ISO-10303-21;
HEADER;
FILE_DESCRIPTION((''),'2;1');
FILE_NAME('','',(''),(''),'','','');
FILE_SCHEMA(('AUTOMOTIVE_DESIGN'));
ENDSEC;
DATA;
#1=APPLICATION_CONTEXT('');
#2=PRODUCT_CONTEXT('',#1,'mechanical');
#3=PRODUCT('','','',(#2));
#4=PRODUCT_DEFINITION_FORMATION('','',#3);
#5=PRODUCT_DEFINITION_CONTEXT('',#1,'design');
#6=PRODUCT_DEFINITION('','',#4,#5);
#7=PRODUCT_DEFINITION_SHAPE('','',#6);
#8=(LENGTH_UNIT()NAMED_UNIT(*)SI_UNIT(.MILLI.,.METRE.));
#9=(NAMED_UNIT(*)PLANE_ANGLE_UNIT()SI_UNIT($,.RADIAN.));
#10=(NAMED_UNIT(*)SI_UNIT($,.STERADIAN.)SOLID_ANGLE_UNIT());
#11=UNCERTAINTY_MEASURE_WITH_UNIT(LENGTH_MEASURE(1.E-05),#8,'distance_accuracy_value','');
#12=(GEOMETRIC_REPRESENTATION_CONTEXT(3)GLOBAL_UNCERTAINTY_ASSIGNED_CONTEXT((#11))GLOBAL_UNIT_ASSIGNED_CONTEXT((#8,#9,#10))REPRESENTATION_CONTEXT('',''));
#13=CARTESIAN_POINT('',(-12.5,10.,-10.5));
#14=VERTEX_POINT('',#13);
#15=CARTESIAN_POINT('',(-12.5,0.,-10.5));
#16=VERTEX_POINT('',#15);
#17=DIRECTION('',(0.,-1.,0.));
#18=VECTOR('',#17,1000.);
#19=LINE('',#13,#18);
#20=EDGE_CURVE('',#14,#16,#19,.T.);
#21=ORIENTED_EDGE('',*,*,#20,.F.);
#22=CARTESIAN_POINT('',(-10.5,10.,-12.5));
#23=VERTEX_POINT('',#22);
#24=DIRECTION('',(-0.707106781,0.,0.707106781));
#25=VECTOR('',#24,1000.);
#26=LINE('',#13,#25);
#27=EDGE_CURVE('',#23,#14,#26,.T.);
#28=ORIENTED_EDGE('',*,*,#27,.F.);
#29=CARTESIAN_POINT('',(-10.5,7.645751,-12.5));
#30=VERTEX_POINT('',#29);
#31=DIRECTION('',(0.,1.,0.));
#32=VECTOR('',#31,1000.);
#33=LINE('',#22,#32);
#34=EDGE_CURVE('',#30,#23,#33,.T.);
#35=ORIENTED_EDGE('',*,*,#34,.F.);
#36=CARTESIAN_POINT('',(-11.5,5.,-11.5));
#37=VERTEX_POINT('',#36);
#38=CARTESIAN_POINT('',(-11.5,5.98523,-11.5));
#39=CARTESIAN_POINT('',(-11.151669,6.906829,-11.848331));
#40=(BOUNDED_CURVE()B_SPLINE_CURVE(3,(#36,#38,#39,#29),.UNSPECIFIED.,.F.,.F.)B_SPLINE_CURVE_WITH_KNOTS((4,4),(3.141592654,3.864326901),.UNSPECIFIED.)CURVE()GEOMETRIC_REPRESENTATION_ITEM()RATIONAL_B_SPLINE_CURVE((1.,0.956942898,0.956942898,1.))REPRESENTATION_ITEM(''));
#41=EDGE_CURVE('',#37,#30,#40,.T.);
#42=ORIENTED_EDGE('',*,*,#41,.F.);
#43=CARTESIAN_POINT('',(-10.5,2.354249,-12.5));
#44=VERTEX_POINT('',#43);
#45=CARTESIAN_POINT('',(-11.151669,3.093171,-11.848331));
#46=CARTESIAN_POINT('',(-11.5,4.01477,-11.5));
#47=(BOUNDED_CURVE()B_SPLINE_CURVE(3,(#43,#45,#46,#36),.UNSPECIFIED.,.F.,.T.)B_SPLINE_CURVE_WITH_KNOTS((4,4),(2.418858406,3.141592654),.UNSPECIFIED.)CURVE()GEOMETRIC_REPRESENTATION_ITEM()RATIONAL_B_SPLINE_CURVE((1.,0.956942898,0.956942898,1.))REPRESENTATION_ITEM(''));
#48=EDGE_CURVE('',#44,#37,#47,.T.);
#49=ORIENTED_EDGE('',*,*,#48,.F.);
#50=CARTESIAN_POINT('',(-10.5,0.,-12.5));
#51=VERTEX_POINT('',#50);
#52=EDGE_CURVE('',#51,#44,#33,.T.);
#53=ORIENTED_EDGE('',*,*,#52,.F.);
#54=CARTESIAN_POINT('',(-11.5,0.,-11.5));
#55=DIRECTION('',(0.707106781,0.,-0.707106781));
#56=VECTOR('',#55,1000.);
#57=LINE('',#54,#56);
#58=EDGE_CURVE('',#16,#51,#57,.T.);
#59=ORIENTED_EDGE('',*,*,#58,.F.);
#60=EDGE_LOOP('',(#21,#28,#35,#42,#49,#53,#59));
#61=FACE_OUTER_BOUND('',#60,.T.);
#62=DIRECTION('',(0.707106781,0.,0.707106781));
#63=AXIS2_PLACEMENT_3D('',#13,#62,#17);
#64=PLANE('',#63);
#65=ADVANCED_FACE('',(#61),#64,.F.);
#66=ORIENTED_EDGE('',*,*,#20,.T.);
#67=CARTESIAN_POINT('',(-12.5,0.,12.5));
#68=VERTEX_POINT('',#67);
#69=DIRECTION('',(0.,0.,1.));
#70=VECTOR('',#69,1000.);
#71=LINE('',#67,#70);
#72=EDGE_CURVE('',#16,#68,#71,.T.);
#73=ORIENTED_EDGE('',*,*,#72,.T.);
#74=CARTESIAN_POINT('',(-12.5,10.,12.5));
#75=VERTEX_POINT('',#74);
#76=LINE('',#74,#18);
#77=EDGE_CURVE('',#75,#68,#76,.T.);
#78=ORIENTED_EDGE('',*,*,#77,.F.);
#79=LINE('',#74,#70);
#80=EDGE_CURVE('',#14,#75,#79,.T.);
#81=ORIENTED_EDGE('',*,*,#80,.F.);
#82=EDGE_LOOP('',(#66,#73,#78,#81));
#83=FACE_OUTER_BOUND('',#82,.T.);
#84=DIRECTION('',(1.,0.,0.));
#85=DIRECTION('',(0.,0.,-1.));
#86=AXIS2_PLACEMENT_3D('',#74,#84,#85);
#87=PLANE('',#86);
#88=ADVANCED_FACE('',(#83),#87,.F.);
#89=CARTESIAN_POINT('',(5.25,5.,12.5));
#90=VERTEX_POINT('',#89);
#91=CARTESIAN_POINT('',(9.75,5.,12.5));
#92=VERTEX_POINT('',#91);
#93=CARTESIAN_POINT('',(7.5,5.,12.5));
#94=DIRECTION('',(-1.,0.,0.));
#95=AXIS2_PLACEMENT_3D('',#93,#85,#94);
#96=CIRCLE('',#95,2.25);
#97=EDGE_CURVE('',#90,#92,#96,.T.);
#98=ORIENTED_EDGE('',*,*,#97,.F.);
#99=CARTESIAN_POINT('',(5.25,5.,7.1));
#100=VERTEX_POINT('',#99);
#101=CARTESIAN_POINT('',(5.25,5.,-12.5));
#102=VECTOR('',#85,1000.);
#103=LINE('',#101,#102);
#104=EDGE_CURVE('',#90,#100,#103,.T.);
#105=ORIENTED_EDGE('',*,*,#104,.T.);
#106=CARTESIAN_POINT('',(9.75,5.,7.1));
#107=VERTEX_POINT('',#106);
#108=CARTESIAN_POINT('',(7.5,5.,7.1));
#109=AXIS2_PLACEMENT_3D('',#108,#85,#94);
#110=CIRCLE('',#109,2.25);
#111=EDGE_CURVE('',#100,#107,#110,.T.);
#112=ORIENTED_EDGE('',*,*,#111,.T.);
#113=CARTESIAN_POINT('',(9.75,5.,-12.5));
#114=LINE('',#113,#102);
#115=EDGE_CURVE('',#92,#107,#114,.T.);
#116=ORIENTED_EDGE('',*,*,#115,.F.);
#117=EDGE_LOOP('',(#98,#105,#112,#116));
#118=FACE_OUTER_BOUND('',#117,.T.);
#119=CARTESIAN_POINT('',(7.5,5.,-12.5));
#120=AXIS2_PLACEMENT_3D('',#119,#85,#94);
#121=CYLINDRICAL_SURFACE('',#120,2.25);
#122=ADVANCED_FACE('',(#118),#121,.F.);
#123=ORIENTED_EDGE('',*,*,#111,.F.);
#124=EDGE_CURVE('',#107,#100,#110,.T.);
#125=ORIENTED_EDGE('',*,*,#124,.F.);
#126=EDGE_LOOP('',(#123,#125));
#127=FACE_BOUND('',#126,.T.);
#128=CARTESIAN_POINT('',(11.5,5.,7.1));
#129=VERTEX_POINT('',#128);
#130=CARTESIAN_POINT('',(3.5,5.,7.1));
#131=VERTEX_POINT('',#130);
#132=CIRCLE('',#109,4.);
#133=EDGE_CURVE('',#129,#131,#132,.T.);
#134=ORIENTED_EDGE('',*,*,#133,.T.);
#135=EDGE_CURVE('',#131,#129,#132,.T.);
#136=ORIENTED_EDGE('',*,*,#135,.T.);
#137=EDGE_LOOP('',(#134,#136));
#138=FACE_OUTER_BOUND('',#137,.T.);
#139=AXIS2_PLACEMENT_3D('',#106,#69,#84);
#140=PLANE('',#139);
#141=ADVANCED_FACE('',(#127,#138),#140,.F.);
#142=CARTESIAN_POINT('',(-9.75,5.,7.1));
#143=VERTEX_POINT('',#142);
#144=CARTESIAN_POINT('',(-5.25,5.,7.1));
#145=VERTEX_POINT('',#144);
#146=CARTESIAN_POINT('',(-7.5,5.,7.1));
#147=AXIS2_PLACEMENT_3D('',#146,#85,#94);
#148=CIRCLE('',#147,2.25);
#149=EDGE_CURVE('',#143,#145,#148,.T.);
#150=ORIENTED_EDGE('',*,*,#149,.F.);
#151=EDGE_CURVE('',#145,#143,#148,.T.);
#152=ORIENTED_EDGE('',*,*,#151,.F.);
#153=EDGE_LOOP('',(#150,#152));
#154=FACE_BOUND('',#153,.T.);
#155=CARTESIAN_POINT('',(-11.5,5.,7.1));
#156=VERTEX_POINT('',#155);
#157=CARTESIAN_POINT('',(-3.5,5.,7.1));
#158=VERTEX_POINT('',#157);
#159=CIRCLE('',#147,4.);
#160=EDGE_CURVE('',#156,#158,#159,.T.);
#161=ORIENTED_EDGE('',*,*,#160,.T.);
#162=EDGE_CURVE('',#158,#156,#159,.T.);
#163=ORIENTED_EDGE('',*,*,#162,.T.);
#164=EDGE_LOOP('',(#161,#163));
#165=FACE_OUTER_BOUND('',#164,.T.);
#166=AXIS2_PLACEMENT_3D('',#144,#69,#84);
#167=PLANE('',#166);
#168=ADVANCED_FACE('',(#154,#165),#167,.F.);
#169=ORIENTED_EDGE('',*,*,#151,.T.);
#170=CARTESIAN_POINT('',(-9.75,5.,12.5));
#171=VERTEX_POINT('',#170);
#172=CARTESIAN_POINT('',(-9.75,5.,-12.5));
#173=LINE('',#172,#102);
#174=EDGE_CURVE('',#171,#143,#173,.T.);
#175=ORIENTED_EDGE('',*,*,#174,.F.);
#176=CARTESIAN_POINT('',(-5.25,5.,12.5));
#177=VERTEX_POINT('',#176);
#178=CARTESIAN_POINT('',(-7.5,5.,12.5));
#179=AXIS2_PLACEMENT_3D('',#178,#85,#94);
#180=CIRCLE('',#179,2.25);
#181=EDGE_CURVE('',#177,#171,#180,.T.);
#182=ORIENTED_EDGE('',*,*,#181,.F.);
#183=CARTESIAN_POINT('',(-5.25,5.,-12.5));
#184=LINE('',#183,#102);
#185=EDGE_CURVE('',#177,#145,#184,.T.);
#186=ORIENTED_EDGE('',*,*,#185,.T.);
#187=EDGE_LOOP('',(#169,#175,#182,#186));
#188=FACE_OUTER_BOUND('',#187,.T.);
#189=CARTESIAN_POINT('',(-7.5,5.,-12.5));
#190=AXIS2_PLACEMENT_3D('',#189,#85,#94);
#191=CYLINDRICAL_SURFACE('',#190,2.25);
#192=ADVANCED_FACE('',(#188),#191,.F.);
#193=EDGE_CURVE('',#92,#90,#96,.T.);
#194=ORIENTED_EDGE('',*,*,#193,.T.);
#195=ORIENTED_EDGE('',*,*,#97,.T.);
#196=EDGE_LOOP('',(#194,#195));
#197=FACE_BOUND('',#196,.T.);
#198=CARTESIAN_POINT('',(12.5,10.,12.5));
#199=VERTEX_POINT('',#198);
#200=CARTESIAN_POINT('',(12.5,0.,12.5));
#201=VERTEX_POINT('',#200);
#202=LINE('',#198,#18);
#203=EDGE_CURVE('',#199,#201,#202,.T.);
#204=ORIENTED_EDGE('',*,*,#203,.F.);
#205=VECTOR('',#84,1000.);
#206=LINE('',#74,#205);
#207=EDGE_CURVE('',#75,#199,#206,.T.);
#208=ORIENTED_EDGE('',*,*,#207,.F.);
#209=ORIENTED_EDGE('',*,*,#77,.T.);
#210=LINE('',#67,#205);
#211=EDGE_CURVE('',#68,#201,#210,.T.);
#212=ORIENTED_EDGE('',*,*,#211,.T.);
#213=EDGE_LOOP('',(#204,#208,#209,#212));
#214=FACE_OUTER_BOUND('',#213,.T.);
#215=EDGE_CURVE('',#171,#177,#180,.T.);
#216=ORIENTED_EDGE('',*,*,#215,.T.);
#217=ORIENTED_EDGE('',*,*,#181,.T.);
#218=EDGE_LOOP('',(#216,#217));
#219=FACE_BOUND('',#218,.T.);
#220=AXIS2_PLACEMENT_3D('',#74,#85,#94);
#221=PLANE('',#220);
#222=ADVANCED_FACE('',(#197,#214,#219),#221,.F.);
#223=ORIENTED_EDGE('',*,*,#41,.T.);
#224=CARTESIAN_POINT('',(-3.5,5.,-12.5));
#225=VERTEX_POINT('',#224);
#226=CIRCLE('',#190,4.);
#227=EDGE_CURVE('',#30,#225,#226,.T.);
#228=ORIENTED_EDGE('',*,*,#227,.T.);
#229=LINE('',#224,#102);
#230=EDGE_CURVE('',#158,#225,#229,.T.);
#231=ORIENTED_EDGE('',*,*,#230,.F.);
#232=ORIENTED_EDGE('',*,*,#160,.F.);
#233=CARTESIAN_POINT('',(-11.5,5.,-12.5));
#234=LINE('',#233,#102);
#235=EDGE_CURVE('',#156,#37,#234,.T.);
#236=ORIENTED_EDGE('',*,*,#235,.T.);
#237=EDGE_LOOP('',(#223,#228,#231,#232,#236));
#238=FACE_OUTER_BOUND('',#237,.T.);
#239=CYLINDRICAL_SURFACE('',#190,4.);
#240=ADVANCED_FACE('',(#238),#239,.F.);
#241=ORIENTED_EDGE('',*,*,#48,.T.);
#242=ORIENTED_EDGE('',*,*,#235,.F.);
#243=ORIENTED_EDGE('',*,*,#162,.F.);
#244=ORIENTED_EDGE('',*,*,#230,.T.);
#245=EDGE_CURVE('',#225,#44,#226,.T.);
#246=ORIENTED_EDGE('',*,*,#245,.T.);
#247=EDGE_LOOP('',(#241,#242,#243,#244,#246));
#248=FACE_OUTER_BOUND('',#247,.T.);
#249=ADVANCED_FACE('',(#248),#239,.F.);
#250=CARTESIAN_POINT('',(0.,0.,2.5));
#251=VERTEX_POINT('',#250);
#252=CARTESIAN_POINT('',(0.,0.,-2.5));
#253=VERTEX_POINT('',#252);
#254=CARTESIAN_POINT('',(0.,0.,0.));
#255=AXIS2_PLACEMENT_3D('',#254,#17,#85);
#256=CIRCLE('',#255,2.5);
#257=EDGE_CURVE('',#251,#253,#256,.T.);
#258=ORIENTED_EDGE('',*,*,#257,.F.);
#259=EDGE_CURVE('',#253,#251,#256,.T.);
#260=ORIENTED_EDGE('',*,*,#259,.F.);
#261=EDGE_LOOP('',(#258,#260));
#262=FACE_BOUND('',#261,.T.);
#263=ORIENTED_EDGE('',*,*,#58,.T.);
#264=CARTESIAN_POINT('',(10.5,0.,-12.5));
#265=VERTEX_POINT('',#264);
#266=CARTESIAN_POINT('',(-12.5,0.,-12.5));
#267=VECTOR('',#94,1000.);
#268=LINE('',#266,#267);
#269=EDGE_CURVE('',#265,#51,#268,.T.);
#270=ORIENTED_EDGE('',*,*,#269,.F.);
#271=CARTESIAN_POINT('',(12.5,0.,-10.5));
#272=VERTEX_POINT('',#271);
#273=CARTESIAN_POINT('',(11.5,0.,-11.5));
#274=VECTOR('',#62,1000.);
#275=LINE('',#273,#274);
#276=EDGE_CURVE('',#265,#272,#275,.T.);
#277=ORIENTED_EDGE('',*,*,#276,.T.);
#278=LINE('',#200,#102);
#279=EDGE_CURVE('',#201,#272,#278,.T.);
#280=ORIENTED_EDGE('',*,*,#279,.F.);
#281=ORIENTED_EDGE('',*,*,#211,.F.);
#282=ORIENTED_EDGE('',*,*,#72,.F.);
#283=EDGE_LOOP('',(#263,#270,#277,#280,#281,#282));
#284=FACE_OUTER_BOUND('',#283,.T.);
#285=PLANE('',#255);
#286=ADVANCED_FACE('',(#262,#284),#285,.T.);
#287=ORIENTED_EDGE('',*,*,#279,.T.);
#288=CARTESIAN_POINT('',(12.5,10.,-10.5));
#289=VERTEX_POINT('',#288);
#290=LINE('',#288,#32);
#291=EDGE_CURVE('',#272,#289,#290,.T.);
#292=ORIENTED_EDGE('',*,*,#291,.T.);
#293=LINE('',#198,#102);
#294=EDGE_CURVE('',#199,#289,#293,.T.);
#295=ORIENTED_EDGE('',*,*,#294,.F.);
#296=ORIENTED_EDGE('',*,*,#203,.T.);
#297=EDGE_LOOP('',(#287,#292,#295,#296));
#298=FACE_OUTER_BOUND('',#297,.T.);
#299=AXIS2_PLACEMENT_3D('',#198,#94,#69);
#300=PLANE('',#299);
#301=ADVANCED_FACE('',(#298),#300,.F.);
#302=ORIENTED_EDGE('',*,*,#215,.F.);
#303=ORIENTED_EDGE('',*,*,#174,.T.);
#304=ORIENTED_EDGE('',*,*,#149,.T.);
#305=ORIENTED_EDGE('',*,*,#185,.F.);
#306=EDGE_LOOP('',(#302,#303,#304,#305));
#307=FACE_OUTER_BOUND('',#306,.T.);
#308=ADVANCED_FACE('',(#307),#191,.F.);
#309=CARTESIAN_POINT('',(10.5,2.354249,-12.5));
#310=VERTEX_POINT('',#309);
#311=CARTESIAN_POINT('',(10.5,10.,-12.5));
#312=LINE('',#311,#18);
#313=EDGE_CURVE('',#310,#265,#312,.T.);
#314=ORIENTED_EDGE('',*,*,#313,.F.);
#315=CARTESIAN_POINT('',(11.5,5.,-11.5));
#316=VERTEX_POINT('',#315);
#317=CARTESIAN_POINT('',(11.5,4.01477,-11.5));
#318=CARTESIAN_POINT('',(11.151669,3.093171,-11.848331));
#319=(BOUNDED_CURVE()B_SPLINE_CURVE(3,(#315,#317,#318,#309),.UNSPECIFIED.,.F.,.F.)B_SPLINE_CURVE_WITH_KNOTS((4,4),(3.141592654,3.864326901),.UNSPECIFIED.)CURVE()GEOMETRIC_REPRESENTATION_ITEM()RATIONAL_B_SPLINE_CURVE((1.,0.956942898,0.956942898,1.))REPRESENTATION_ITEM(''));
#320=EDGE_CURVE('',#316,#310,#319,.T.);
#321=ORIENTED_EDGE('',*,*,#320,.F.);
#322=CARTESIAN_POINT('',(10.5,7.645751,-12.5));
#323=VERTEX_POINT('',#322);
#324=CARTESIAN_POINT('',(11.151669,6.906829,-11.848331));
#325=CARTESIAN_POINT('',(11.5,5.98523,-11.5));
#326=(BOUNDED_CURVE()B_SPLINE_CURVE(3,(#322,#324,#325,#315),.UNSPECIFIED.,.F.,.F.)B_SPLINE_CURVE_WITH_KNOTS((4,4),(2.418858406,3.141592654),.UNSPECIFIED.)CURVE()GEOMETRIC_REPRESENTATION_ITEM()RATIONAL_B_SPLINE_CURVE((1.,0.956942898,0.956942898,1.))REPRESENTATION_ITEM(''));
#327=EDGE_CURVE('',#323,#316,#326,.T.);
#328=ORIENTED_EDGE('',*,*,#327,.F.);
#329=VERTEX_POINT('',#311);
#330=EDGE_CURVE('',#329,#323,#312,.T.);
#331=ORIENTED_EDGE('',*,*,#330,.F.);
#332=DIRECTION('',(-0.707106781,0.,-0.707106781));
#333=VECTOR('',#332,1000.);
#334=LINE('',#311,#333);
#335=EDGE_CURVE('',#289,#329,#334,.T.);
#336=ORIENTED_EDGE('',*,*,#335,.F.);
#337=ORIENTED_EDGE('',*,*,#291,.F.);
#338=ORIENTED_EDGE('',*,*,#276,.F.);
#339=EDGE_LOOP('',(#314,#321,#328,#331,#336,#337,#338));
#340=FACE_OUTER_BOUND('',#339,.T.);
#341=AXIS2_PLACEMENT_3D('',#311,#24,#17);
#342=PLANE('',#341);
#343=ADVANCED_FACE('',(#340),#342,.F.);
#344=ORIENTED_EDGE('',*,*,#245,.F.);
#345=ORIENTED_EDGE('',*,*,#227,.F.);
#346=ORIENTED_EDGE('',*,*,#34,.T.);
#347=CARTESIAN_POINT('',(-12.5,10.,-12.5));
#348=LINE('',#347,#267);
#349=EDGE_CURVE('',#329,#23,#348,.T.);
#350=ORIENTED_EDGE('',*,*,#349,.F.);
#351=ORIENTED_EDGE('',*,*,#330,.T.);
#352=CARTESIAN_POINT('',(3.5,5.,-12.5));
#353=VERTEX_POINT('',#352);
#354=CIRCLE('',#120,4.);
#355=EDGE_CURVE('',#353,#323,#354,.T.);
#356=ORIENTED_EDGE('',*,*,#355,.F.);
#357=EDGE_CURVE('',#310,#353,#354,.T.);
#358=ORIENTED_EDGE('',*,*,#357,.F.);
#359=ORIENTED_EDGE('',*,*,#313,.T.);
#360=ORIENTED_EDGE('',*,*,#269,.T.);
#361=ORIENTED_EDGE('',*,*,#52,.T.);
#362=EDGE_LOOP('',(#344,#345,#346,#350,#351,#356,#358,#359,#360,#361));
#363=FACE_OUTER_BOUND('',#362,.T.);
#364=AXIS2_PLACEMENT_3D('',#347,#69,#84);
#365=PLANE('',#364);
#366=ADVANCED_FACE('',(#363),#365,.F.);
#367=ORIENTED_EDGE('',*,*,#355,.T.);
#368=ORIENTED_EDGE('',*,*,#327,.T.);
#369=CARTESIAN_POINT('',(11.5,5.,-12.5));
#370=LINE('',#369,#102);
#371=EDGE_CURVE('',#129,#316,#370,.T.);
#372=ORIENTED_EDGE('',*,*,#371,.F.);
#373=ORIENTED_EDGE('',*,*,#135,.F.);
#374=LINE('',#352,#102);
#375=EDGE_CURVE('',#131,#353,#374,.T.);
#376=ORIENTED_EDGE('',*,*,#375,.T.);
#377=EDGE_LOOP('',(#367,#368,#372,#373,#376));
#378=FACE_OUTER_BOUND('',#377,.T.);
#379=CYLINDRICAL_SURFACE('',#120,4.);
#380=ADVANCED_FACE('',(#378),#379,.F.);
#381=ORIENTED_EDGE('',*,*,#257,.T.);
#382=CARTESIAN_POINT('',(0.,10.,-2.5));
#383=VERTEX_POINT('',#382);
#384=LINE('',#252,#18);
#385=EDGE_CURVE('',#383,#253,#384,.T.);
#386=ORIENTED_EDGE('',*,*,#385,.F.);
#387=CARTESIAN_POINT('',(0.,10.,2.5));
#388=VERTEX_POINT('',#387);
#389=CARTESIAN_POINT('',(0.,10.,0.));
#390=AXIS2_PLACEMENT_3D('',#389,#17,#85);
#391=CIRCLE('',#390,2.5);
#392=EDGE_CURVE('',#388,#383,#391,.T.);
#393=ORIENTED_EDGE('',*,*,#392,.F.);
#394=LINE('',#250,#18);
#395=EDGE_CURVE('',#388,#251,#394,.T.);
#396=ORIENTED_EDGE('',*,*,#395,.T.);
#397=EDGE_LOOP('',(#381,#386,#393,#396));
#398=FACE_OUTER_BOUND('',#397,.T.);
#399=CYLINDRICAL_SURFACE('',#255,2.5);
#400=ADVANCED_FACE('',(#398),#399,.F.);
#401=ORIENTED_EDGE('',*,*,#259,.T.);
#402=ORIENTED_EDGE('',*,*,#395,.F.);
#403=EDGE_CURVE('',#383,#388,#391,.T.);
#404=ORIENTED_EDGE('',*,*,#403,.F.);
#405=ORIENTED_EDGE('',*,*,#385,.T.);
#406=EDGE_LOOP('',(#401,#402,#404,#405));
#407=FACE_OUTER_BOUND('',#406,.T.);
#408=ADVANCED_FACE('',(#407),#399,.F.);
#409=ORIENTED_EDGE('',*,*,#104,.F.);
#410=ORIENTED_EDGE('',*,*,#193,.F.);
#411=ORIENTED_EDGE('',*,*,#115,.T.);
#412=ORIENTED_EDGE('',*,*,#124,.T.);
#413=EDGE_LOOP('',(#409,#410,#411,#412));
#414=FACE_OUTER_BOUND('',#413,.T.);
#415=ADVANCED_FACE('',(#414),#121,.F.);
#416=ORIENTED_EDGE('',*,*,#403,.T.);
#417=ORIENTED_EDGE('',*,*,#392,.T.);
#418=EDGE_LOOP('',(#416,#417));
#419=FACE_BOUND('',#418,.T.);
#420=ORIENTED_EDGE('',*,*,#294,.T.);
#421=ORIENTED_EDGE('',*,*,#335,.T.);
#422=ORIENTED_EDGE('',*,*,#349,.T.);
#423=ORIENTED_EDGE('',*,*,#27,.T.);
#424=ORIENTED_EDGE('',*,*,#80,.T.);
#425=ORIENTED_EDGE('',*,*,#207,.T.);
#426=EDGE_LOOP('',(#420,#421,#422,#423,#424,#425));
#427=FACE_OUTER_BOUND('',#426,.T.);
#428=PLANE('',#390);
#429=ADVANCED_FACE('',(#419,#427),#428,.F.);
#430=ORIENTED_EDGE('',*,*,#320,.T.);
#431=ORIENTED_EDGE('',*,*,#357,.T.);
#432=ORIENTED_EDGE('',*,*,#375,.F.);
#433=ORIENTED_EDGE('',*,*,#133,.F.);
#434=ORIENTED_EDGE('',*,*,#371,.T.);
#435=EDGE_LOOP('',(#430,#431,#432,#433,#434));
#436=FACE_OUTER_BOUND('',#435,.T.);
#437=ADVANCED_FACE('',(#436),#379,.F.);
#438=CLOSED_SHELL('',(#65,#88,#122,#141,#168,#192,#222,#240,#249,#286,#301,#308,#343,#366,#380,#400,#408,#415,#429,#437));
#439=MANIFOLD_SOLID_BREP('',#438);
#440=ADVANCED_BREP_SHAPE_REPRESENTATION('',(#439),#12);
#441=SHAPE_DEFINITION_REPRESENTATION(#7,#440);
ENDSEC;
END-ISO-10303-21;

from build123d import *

# Parameters (mm, degrees)
SKETCH_1_W                   = 25
SKETCH_1_H                   = 25
EXTRUDE_1_DEPTH              = 10
CHAMFER_1_SIZE               = 2
HOLE_WIZARD_M6_1_D           = 5
HOLE_WIZARD_M4_1_D           = 4.5
HOLE_WIZARD_M4_1_CBORE_D     = 8
HOLE_WIZARD_M4_1_CBORE_DEPTH = 19.6


with BuildPart() as part:
    # 草图1 → 凸台-拉伸1 (new body)
    with BuildSketch(Plane(origin=(0, 0, 0), x_dir=(1, 0, 0), z_dir=(0, 1, 0))):
        Rectangle(SKETCH_1_W, SKETCH_1_H)
    extrude(amount=EXTRUDE_1_DEPTH)

    # 倒角1
    chamfer_1_edges = [part.edges().sort_by_distance(p)[0] for p in [
        (-12.5, 5, -12.5),
        (12.5, 5, -12.5),
    ]]
    chamfer(chamfer_1_edges, length=CHAMFER_1_SIZE)

    # M6 螺纹孔1 (through all)
    with Locations(Plane(origin=(0, 0, 0), x_dir=(-1, 0, 0), z_dir=(0, -1, 0))):
        with Locations((0, 0)):
            Hole(HOLE_WIZARD_M6_1_D / 2)

    # M4 六角圆柱头螺钉的柱形沉头孔1 (through all)
    with Locations(Plane(origin=(0, 0, -12.5), x_dir=(-1, 0, 0), z_dir=(0, 0, -1))):
        with Locations((-7.5, 5), (7.5, 5)):
            CounterBoreHole(HOLE_WIZARD_M4_1_D / 2, HOLE_WIZARD_M4_1_CBORE_D / 2, HOLE_WIZARD_M4_1_CBORE_DEPTH)


solid = part.part
